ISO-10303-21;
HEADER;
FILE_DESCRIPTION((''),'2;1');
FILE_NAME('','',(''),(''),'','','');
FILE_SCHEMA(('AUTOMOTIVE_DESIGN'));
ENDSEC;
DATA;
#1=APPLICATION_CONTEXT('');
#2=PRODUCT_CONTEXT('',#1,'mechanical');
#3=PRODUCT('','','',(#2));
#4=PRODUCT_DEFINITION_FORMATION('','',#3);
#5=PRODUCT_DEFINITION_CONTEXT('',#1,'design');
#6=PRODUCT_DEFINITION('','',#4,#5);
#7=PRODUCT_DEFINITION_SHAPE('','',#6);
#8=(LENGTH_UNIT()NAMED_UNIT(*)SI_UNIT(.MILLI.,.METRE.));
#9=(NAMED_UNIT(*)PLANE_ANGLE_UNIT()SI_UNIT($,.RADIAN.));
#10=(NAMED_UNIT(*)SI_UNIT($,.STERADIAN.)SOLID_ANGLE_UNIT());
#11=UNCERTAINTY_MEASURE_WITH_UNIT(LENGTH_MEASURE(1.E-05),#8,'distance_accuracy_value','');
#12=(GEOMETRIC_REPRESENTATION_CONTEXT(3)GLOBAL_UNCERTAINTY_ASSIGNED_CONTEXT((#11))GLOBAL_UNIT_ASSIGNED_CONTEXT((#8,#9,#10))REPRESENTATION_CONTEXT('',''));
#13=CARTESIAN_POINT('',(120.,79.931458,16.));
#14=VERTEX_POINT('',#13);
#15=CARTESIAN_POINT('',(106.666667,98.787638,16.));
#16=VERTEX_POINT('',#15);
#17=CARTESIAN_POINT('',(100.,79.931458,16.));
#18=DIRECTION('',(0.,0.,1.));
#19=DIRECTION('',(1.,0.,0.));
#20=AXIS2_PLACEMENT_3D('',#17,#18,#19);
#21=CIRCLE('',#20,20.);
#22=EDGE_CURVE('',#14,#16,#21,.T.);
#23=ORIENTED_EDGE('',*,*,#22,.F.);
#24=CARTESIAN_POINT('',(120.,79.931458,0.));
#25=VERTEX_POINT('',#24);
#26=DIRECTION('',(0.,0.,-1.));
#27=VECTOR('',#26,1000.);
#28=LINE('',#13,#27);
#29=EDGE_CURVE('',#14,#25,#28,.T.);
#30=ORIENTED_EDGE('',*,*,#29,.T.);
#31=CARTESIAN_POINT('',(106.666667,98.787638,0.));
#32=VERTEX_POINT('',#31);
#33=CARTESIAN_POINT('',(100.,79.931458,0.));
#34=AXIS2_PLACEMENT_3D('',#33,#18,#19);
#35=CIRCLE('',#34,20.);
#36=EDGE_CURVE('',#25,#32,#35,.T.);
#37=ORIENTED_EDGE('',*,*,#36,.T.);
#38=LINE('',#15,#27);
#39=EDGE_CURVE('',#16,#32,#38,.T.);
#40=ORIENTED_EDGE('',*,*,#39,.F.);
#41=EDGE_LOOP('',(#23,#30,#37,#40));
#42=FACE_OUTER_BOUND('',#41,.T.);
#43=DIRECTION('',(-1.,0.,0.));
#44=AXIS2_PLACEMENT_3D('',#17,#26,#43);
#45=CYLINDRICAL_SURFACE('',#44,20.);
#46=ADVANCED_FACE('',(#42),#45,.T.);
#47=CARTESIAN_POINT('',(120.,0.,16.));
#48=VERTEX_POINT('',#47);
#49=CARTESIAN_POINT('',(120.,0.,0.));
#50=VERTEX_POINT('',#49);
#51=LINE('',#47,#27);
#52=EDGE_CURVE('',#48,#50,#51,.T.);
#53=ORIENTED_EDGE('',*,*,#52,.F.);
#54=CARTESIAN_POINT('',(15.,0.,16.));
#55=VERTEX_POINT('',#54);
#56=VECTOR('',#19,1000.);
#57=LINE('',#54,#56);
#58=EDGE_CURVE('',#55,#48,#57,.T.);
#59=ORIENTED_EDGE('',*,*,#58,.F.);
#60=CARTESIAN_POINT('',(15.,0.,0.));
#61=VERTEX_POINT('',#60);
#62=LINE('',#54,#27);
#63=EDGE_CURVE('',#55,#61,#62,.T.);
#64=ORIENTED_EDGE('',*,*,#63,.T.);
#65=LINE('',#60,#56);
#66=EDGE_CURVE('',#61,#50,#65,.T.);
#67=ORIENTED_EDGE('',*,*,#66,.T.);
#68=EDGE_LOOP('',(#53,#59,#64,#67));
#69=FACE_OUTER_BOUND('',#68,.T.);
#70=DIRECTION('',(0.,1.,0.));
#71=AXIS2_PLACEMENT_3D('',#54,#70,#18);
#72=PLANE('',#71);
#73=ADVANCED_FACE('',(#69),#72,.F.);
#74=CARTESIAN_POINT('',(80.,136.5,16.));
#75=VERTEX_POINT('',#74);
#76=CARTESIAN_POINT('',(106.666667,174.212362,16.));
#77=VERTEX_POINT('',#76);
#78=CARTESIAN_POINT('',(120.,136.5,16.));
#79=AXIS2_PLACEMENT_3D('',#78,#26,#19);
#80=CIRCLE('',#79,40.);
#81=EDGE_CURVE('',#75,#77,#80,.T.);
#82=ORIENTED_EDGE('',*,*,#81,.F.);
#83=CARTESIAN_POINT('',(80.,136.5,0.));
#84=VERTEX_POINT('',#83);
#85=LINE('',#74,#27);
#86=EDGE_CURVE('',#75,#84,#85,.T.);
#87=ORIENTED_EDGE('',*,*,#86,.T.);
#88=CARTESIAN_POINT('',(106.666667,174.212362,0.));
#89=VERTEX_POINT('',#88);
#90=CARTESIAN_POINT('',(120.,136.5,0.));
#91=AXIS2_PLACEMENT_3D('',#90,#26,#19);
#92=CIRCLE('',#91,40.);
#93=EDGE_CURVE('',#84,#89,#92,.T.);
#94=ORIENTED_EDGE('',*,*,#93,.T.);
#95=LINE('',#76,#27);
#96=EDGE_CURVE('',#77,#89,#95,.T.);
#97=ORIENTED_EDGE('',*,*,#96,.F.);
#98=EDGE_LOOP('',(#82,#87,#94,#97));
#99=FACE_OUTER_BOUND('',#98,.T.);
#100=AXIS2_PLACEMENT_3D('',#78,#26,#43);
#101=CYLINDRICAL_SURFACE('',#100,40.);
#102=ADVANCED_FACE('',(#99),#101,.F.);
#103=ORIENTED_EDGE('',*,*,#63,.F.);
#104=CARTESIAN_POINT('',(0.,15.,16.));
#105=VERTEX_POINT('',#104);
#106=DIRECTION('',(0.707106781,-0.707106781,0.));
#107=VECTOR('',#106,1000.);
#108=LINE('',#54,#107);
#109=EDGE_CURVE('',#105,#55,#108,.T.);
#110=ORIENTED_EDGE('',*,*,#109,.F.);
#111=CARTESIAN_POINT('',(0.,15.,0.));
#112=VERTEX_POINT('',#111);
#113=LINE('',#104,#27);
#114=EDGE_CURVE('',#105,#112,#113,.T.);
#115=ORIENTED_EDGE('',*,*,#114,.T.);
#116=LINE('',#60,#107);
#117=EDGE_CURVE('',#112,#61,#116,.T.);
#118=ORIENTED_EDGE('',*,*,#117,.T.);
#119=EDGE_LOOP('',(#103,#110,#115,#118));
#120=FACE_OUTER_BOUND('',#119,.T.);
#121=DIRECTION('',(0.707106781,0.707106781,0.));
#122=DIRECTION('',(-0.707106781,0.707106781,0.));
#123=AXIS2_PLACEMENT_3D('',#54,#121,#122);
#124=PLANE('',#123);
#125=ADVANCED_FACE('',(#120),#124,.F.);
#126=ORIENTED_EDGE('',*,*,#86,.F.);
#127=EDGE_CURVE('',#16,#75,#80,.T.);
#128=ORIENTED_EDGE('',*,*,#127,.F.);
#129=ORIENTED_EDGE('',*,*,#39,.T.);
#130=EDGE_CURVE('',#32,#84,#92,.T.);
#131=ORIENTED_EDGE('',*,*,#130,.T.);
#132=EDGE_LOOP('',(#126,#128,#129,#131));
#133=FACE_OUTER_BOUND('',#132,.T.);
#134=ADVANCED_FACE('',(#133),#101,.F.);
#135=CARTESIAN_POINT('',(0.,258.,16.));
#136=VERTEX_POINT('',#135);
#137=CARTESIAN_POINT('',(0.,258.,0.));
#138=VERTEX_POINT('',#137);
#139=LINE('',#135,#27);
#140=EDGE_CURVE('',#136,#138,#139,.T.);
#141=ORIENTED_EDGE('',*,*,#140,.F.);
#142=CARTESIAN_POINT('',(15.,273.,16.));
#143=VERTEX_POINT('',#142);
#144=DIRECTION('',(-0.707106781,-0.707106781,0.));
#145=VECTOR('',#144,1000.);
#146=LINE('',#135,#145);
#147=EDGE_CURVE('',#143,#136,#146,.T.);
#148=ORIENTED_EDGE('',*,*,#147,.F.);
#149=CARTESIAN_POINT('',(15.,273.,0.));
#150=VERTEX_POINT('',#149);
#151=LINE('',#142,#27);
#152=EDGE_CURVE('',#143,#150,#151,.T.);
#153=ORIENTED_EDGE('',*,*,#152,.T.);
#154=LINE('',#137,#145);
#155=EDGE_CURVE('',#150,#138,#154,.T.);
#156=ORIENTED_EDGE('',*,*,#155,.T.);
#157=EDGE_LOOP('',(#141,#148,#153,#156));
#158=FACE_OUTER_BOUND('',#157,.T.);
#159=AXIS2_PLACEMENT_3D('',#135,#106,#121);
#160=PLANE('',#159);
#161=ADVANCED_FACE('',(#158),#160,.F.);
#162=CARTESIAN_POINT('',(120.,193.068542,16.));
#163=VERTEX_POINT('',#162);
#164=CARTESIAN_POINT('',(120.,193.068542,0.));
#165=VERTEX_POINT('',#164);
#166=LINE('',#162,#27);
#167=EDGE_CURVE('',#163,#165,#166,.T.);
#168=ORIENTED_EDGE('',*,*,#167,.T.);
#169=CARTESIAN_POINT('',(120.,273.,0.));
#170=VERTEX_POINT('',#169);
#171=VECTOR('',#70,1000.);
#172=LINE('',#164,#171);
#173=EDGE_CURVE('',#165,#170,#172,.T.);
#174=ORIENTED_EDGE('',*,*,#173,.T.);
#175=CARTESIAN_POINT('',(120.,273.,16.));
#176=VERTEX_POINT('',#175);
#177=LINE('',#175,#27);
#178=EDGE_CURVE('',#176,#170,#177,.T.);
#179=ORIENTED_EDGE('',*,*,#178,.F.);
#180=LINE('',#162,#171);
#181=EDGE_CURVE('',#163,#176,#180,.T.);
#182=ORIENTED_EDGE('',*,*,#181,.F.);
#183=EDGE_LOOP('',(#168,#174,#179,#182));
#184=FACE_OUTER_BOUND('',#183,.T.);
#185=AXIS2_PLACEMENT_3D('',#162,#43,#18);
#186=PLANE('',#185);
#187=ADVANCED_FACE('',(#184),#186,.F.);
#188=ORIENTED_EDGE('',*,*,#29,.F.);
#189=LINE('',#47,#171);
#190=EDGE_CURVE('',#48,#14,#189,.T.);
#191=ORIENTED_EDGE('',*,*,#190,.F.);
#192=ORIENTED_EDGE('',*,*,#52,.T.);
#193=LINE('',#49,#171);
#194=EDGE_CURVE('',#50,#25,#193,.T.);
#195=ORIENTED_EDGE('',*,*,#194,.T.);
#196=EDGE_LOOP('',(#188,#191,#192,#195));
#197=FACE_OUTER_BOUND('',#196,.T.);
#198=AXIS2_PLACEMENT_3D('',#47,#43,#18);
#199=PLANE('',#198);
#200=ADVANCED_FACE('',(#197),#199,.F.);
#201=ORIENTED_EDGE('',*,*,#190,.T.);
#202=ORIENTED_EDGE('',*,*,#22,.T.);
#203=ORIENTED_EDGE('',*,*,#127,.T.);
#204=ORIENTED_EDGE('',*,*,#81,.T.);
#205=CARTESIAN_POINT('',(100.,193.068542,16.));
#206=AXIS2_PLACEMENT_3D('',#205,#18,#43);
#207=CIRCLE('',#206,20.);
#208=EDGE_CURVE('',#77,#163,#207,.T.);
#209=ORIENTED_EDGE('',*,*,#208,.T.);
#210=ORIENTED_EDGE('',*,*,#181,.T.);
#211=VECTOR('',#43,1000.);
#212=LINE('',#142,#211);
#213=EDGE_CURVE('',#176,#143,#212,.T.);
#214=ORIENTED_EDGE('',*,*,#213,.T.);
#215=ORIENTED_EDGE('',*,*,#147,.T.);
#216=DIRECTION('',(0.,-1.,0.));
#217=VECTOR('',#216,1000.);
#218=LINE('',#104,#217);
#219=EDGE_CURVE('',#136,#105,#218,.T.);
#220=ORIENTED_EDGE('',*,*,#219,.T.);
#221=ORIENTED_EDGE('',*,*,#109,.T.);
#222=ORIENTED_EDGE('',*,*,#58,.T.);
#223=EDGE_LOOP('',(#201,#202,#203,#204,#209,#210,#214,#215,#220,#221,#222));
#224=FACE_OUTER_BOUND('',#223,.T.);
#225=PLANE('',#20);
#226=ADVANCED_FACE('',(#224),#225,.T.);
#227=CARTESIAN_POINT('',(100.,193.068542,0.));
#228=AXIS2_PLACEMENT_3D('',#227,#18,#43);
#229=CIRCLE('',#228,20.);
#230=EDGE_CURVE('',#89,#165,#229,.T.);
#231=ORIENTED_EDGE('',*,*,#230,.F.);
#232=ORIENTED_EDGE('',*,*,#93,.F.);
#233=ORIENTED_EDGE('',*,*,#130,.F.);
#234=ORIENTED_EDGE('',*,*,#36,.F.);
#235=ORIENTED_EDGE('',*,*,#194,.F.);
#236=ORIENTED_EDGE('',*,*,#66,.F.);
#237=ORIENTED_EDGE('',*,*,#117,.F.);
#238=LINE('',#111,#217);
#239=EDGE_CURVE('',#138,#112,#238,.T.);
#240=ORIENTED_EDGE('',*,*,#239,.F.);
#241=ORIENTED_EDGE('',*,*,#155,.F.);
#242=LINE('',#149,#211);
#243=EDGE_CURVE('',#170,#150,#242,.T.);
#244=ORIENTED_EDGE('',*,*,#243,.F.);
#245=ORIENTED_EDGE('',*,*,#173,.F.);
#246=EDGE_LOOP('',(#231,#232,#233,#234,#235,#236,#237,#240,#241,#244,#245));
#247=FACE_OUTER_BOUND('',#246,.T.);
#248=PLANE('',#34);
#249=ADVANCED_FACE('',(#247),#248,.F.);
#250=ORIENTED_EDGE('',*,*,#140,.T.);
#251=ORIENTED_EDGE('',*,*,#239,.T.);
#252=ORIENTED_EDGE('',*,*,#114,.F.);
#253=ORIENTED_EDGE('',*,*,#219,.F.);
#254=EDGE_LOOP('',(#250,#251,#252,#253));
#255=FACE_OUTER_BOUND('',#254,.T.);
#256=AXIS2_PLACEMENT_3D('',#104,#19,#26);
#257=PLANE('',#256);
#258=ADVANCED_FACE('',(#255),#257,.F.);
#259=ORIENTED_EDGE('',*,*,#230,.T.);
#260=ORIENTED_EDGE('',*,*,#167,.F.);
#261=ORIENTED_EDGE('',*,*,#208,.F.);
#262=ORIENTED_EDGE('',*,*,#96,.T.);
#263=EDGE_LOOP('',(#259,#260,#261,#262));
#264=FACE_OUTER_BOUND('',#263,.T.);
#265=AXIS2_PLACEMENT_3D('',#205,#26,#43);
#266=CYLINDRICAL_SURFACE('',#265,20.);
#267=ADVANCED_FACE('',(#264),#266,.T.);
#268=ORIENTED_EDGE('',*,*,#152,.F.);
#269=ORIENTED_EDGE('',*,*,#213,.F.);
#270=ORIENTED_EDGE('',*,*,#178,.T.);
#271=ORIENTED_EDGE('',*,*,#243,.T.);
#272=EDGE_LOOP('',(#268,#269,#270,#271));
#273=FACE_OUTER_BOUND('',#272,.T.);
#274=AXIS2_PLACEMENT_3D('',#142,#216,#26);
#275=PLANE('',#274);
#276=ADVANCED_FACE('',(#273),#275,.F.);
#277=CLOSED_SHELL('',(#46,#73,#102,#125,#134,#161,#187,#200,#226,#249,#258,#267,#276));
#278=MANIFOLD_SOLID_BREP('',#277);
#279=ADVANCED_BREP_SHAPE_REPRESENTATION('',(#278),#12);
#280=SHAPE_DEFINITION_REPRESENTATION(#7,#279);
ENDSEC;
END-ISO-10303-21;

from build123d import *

# Parameters (mm, degrees)
BOSS_EXTRUDE1_DEPTH = 16


with BuildPart() as part:
    # Sketch1 → Boss-Extrude1 (new body)
    with BuildSketch(Plane.XY):
        with BuildLine():
            Line((0, 258), (15, 273))
            Line((15, 273), (120, 273))
            Line((120, 273), (120, 193.068542495))
            ThreePointArc((120, 193.068542495), (116.329931619, 181.521537111), (106.666666667, 174.212361663))
            ThreePointArc((106.666666667, 174.212361663), (80, 136.5), (106.666666667, 98.787638337))
            ThreePointArc((106.666666667, 98.787638337), (116.329931619, 91.478462889), (120, 79.931457505))
            Line((120, 79.931457505), (120, 0))
            Line((120, 0), (15, 0))
            Line((15, 0), (0, 15))
            Line((0, 15), (0, 258))
        make_face()
    extrude(amount=BOSS_EXTRUDE1_DEPTH)


solid = part.part
